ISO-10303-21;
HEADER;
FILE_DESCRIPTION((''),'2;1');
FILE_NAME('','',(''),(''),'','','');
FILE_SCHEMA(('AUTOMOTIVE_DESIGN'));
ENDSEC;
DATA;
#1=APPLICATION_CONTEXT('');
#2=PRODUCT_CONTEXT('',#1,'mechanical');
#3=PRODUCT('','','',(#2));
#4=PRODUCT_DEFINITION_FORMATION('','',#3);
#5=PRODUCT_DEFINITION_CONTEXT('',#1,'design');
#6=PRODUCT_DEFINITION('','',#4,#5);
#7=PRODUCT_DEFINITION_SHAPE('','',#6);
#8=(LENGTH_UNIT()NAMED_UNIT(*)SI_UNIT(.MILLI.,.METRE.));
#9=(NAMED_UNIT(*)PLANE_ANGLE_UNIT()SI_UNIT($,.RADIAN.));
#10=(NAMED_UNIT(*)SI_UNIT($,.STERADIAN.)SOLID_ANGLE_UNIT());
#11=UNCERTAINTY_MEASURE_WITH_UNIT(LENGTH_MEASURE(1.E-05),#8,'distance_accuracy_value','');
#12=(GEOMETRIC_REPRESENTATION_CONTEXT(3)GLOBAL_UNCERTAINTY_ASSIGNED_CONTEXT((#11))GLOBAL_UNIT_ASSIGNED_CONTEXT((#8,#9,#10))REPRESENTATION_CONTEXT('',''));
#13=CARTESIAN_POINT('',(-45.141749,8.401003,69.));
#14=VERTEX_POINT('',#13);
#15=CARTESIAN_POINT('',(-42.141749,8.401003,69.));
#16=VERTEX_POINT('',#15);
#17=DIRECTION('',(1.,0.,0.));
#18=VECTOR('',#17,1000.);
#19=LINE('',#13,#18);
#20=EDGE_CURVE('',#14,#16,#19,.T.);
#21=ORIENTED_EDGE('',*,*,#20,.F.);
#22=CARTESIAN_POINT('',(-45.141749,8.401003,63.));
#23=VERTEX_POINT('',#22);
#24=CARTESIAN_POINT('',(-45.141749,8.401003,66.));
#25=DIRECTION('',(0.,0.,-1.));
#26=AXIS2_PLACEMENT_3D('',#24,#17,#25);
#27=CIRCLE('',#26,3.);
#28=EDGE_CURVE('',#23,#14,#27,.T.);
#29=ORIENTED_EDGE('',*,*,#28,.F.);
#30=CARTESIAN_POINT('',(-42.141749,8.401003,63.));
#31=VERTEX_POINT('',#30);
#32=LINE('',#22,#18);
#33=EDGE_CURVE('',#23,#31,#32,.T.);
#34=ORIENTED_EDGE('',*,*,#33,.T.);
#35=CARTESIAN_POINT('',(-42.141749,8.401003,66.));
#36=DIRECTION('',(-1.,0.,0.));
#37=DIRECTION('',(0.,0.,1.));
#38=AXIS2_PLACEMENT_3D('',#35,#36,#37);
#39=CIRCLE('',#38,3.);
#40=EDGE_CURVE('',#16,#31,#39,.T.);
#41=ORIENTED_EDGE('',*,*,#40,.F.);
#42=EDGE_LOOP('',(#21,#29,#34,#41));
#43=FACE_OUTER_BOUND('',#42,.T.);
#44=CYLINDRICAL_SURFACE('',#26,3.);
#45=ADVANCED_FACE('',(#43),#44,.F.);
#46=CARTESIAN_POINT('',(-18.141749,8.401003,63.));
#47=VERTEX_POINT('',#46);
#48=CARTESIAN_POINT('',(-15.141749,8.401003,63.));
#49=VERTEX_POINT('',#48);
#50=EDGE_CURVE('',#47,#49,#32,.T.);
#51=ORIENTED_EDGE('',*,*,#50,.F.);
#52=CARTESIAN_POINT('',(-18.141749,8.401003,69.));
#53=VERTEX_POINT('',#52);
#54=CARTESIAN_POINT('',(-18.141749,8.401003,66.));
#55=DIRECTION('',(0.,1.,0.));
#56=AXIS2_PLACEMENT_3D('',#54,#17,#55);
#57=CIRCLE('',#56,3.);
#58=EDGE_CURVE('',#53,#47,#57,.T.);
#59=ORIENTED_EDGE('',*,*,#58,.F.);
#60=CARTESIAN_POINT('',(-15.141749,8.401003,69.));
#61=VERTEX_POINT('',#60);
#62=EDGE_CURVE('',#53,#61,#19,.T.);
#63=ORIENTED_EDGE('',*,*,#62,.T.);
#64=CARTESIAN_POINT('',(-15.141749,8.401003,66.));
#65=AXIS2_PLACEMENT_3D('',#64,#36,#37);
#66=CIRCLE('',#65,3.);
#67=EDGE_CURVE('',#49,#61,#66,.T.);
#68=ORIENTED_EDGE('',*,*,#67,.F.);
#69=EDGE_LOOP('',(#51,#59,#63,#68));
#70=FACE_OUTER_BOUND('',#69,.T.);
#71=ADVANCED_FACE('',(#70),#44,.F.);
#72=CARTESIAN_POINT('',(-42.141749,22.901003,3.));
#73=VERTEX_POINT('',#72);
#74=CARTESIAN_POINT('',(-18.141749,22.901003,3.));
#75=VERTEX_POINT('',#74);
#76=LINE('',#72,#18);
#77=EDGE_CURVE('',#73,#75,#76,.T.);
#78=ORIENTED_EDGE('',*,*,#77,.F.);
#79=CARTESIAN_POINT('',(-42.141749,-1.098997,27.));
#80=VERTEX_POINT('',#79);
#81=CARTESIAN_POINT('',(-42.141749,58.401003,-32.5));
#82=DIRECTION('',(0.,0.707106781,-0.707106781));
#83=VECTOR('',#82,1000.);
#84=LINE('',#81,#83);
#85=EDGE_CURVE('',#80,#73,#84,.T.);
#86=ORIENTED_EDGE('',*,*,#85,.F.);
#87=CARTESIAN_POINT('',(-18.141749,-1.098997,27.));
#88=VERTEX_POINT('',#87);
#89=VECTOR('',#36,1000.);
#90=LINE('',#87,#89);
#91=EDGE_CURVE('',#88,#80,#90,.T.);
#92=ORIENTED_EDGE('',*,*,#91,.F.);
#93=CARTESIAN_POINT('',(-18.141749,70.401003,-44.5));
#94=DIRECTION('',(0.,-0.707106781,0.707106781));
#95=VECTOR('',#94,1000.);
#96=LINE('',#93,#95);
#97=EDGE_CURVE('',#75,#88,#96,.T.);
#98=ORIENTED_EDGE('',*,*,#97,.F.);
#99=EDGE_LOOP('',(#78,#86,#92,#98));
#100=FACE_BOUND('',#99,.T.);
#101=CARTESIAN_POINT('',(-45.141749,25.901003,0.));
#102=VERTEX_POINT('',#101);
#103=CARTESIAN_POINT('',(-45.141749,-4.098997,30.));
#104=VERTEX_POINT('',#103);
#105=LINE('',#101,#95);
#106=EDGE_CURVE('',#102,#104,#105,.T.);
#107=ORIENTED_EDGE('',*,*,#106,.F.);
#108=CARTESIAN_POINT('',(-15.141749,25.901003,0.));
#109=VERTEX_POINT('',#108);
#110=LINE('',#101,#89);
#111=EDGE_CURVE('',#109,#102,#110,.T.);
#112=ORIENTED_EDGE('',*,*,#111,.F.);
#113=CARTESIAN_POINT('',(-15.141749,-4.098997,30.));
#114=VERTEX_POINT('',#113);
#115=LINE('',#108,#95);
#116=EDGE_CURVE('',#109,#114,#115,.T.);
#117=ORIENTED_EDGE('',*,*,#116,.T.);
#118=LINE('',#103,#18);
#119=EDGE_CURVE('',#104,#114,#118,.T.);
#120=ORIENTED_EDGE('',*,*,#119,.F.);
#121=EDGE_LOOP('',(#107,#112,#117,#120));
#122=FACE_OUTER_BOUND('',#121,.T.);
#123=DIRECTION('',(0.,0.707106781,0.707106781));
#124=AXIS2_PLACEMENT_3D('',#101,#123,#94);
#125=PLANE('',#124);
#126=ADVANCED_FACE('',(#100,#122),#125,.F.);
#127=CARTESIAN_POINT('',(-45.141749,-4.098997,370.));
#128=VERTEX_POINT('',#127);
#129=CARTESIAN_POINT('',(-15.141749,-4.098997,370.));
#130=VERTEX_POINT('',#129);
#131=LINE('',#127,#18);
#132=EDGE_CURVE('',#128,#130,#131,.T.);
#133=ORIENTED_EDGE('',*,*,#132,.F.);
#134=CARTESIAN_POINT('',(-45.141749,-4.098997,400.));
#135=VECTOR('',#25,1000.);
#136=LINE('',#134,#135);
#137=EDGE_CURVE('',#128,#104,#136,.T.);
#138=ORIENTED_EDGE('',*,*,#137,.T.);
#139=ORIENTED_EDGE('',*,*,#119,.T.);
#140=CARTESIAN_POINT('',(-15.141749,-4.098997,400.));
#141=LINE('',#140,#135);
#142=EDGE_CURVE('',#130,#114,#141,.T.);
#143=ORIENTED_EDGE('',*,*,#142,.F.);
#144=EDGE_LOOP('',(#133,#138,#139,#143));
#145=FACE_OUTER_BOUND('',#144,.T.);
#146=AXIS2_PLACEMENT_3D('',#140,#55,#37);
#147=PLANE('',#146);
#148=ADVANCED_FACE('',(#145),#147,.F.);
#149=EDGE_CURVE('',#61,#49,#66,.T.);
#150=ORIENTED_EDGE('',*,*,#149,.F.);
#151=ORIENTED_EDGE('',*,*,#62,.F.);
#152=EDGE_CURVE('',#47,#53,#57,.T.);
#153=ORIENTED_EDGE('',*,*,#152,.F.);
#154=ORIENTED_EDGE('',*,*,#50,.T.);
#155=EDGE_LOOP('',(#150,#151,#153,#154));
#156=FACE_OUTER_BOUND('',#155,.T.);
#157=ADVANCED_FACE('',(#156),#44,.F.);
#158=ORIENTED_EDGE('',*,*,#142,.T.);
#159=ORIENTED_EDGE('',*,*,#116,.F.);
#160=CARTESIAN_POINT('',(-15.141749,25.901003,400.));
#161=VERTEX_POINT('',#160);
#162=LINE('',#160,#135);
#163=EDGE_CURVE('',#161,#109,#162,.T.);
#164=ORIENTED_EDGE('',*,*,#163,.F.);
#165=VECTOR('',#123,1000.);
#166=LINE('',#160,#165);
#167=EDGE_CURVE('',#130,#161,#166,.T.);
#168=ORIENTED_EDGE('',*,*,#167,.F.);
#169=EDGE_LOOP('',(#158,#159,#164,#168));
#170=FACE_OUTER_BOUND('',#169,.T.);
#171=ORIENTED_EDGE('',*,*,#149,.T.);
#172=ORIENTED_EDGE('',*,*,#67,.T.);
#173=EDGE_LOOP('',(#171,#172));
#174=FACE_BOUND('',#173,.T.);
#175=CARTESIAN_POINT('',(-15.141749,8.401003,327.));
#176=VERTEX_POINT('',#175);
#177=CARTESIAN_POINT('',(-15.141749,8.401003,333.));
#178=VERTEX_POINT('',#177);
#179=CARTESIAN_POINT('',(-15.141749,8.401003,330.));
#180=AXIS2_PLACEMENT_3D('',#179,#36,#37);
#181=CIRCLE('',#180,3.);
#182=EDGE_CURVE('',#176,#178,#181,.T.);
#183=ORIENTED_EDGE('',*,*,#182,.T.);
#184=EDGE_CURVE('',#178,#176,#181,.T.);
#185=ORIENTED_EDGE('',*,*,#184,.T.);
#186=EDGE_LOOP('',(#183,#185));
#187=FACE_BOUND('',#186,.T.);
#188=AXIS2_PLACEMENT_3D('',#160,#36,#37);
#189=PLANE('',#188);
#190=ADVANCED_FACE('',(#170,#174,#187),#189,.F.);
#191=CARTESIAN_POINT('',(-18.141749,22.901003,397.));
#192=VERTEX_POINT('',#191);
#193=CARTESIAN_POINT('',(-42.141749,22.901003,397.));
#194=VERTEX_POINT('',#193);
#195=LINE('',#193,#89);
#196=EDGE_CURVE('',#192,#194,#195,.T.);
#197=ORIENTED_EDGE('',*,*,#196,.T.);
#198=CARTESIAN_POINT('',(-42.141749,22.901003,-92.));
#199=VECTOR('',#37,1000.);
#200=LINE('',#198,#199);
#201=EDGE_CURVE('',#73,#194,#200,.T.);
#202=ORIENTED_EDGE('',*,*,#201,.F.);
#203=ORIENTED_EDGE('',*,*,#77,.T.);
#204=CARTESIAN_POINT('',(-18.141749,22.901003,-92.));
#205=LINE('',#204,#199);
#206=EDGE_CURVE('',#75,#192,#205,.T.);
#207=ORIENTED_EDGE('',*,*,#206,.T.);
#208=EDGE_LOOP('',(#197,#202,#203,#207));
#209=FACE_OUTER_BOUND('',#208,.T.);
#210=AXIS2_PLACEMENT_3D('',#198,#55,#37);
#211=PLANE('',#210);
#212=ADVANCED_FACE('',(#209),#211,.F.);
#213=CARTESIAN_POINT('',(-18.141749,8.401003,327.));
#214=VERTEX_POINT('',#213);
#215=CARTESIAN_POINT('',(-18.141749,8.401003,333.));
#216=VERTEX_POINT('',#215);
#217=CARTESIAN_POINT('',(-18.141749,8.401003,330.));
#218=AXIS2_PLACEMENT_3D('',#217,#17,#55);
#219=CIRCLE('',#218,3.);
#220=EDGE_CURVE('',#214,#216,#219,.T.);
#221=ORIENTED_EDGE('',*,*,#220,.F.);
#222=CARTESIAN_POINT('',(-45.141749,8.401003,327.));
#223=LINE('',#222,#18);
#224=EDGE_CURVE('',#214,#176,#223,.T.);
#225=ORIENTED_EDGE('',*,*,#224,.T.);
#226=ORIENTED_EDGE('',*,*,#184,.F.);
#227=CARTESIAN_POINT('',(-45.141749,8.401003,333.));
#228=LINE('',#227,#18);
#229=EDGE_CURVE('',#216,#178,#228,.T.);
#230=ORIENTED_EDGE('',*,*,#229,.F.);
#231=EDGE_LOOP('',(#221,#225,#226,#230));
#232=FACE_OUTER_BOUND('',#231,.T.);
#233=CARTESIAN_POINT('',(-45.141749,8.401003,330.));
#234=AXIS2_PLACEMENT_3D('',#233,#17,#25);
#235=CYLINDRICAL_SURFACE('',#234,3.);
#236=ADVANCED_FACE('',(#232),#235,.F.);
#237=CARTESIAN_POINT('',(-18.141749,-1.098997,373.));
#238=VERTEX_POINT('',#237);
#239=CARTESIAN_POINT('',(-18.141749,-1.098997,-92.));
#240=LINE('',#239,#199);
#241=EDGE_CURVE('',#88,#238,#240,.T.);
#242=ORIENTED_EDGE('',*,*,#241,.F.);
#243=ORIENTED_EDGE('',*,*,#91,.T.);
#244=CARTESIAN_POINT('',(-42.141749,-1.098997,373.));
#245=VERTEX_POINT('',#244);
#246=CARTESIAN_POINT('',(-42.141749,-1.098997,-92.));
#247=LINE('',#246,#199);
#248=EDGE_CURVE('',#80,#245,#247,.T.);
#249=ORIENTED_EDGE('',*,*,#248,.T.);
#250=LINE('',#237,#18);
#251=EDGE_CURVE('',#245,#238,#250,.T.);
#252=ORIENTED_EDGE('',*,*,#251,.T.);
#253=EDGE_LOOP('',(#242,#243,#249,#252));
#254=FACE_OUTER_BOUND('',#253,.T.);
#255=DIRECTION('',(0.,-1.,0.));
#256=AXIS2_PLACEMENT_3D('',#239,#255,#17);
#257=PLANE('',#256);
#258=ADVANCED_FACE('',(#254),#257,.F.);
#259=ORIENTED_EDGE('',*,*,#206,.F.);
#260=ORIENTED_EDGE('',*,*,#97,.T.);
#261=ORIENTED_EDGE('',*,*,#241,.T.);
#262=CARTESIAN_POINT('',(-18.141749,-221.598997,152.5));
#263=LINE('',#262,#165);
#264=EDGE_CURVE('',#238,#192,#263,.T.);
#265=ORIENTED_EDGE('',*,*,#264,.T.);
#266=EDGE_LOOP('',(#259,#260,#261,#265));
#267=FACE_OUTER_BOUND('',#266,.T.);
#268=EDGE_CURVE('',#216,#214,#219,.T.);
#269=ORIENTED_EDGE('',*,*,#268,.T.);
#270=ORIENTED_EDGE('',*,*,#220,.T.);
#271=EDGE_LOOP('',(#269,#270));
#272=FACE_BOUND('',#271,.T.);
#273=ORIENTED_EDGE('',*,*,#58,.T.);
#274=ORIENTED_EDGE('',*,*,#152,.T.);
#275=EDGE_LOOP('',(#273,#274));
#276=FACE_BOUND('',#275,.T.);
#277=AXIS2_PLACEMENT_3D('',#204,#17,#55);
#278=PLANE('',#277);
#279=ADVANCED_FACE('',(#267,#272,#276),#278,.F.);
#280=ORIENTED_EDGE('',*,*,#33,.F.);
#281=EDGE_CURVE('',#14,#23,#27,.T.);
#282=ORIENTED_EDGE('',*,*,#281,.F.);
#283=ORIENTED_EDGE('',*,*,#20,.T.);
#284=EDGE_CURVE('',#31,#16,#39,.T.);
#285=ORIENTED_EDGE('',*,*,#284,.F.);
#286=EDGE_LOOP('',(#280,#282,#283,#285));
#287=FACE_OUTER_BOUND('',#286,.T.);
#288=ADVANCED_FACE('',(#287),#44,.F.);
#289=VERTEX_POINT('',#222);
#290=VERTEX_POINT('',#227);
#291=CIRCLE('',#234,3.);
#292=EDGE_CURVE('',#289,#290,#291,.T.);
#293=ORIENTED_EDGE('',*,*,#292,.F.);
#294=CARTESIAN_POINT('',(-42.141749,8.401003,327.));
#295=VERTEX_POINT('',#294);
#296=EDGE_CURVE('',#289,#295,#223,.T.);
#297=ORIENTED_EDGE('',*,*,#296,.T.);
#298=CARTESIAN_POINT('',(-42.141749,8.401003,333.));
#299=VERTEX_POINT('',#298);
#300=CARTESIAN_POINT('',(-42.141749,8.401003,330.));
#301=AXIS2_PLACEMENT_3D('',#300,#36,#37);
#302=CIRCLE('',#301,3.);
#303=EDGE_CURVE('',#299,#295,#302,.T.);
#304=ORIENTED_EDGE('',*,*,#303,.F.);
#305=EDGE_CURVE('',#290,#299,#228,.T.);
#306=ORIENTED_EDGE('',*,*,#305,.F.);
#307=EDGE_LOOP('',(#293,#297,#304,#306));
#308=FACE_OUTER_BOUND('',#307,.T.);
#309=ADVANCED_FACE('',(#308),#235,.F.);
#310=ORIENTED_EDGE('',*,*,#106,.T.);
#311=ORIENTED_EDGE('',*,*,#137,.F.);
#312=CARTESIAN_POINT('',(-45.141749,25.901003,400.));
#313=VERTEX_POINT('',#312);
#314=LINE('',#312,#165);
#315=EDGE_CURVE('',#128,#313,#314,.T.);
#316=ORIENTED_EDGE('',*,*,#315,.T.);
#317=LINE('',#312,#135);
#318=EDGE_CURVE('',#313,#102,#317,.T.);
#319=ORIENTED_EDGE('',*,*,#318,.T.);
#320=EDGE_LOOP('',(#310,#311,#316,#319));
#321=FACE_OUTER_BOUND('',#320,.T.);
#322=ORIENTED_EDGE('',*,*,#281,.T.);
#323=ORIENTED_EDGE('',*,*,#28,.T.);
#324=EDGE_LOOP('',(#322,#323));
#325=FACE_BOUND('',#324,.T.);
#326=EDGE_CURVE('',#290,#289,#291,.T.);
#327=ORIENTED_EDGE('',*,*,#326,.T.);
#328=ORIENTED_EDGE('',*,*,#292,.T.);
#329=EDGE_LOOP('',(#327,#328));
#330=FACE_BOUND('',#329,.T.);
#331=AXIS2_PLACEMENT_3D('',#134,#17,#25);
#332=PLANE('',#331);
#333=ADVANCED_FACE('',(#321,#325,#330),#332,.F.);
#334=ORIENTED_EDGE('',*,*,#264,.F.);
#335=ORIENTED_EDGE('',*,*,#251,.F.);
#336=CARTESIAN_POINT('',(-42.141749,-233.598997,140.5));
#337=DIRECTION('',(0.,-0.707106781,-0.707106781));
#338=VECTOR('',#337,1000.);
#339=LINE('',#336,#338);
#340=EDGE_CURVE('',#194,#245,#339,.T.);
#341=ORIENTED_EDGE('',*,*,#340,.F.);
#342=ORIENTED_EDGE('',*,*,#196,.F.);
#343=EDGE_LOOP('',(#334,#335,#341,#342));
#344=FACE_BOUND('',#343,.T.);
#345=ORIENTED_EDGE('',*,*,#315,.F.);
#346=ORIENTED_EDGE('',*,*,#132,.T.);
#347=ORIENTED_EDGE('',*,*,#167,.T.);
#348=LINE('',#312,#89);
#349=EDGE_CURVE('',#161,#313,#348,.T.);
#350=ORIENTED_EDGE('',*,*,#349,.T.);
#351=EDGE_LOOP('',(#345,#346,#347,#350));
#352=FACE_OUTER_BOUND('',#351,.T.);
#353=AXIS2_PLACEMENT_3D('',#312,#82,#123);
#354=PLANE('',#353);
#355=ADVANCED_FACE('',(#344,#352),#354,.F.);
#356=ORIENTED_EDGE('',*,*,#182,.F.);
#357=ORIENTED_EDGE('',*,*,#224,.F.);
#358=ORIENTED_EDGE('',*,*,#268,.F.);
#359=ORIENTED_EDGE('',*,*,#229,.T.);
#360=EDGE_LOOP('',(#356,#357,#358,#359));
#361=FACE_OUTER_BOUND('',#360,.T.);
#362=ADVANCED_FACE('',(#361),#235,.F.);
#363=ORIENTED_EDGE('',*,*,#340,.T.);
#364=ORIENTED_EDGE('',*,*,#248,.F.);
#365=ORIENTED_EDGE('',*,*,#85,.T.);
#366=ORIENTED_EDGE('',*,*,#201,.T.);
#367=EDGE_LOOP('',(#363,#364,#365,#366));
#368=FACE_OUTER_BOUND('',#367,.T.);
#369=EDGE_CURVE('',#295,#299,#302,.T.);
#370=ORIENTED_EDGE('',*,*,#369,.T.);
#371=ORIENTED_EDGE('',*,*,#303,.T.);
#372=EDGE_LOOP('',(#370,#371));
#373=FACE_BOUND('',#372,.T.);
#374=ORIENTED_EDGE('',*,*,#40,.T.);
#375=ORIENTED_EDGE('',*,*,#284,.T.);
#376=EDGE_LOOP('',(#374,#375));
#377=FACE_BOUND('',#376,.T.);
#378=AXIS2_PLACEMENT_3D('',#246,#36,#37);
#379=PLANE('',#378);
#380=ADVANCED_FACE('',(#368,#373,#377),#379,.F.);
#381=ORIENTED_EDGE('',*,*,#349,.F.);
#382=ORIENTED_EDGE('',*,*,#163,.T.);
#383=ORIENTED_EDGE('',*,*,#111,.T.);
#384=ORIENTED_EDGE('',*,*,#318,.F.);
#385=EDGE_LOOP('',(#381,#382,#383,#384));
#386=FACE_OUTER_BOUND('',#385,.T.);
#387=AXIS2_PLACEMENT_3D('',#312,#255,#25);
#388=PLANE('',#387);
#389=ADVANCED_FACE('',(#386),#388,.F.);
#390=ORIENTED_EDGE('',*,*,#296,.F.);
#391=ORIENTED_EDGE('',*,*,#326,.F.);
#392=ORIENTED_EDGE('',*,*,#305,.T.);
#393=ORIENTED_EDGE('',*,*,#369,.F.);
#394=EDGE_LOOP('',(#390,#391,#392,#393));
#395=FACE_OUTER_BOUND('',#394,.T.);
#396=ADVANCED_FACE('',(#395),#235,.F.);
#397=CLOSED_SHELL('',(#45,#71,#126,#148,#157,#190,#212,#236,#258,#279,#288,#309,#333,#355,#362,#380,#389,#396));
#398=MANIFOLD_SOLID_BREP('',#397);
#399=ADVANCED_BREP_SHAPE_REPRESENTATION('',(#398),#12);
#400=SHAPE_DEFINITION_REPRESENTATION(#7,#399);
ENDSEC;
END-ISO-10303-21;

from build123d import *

# Parameters (mm, degrees)
SKETCH1_W               = 30
SKETCH1_H               = 30
BOSS_EXTRUDE1_DEPTH     = 400
SKETCH2_W               = 24
SKETCH2_H               = 24
CUT_EXTRUDE1_DEPTH      = 492
CUT_EXTRUDE3_DEPTH      = 402.958781438
CUT_EXTRUDE6_DEPTH      = 402.958781438
CUT_EXTRUDE7_DEPTH      = 402.958781438
CUT_EXTRUDE7_DEPTH_BACK = 402.958781438
SKETCH11_R              = 3


with BuildPart() as part:
    # Sketch1 → Boss-Extrude1 (new body)
    with BuildSketch(Plane.XY):
        with Locations((-30.141748722, 10.901003365)):
            Rectangle(SKETCH1_W, SKETCH1_H)
    extrude(amount=BOSS_EXTRUDE1_DEPTH)

    # Sketch2 → Cut-Extrude1 (cut)
    with BuildSketch(Plane.XY.offset(400)):
        with Locations((-30.141748722, 10.901003365)):
            Rectangle(SKETCH2_W, SKETCH2_H)
    extrude(amount=-CUT_EXTRUDE1_DEPTH, mode=Mode.SUBTRACT)

    # Sketch4 → Cut-Extrude3 (cut, through all)
    with BuildSketch(Plane(origin=(-15.141748722, 0, 0), x_dir=(0, 0, -1), z_dir=(1, 0, 0))):
        Polygon((0, 25.901003365), (-30, -4.098996635), (0, -4.098996635), align=None)
    extrude(amount=-CUT_EXTRUDE3_DEPTH, mode=Mode.SUBTRACT)

    # Sketch8 → Cut-Extrude6 (cut, through all)
    with BuildSketch(Plane(origin=(-15.141748722, 0, 0), x_dir=(0, 0, -1), z_dir=(1, 0, 0))):
        Polygon((-400, 25.901003365), (-370, -4.098996635), (-400, -4.098996635), align=None)
    extrude(amount=-CUT_EXTRUDE6_DEPTH, mode=Mode.SUBTRACT)

    # Sketch11 → Cut-Extrude7 (cut, two sides: drawn at the far end of the back side and taken through both)
    with BuildSketch(Plane(origin=(-15.141748722, 0, 0), x_dir=(0, 0, -1), z_dir=(1, 0, 0)).offset(-CUT_EXTRUDE7_DEPTH_BACK)):
        with Locations((-330, 8.401003365)):
            Circle(SKETCH11_R)
        with Locations((-66, 8.401003365)):
            Circle(SKETCH11_R)
    extrude(amount=CUT_EXTRUDE7_DEPTH + CUT_EXTRUDE7_DEPTH_BACK, mode=Mode.SUBTRACT)


solid = part.part
